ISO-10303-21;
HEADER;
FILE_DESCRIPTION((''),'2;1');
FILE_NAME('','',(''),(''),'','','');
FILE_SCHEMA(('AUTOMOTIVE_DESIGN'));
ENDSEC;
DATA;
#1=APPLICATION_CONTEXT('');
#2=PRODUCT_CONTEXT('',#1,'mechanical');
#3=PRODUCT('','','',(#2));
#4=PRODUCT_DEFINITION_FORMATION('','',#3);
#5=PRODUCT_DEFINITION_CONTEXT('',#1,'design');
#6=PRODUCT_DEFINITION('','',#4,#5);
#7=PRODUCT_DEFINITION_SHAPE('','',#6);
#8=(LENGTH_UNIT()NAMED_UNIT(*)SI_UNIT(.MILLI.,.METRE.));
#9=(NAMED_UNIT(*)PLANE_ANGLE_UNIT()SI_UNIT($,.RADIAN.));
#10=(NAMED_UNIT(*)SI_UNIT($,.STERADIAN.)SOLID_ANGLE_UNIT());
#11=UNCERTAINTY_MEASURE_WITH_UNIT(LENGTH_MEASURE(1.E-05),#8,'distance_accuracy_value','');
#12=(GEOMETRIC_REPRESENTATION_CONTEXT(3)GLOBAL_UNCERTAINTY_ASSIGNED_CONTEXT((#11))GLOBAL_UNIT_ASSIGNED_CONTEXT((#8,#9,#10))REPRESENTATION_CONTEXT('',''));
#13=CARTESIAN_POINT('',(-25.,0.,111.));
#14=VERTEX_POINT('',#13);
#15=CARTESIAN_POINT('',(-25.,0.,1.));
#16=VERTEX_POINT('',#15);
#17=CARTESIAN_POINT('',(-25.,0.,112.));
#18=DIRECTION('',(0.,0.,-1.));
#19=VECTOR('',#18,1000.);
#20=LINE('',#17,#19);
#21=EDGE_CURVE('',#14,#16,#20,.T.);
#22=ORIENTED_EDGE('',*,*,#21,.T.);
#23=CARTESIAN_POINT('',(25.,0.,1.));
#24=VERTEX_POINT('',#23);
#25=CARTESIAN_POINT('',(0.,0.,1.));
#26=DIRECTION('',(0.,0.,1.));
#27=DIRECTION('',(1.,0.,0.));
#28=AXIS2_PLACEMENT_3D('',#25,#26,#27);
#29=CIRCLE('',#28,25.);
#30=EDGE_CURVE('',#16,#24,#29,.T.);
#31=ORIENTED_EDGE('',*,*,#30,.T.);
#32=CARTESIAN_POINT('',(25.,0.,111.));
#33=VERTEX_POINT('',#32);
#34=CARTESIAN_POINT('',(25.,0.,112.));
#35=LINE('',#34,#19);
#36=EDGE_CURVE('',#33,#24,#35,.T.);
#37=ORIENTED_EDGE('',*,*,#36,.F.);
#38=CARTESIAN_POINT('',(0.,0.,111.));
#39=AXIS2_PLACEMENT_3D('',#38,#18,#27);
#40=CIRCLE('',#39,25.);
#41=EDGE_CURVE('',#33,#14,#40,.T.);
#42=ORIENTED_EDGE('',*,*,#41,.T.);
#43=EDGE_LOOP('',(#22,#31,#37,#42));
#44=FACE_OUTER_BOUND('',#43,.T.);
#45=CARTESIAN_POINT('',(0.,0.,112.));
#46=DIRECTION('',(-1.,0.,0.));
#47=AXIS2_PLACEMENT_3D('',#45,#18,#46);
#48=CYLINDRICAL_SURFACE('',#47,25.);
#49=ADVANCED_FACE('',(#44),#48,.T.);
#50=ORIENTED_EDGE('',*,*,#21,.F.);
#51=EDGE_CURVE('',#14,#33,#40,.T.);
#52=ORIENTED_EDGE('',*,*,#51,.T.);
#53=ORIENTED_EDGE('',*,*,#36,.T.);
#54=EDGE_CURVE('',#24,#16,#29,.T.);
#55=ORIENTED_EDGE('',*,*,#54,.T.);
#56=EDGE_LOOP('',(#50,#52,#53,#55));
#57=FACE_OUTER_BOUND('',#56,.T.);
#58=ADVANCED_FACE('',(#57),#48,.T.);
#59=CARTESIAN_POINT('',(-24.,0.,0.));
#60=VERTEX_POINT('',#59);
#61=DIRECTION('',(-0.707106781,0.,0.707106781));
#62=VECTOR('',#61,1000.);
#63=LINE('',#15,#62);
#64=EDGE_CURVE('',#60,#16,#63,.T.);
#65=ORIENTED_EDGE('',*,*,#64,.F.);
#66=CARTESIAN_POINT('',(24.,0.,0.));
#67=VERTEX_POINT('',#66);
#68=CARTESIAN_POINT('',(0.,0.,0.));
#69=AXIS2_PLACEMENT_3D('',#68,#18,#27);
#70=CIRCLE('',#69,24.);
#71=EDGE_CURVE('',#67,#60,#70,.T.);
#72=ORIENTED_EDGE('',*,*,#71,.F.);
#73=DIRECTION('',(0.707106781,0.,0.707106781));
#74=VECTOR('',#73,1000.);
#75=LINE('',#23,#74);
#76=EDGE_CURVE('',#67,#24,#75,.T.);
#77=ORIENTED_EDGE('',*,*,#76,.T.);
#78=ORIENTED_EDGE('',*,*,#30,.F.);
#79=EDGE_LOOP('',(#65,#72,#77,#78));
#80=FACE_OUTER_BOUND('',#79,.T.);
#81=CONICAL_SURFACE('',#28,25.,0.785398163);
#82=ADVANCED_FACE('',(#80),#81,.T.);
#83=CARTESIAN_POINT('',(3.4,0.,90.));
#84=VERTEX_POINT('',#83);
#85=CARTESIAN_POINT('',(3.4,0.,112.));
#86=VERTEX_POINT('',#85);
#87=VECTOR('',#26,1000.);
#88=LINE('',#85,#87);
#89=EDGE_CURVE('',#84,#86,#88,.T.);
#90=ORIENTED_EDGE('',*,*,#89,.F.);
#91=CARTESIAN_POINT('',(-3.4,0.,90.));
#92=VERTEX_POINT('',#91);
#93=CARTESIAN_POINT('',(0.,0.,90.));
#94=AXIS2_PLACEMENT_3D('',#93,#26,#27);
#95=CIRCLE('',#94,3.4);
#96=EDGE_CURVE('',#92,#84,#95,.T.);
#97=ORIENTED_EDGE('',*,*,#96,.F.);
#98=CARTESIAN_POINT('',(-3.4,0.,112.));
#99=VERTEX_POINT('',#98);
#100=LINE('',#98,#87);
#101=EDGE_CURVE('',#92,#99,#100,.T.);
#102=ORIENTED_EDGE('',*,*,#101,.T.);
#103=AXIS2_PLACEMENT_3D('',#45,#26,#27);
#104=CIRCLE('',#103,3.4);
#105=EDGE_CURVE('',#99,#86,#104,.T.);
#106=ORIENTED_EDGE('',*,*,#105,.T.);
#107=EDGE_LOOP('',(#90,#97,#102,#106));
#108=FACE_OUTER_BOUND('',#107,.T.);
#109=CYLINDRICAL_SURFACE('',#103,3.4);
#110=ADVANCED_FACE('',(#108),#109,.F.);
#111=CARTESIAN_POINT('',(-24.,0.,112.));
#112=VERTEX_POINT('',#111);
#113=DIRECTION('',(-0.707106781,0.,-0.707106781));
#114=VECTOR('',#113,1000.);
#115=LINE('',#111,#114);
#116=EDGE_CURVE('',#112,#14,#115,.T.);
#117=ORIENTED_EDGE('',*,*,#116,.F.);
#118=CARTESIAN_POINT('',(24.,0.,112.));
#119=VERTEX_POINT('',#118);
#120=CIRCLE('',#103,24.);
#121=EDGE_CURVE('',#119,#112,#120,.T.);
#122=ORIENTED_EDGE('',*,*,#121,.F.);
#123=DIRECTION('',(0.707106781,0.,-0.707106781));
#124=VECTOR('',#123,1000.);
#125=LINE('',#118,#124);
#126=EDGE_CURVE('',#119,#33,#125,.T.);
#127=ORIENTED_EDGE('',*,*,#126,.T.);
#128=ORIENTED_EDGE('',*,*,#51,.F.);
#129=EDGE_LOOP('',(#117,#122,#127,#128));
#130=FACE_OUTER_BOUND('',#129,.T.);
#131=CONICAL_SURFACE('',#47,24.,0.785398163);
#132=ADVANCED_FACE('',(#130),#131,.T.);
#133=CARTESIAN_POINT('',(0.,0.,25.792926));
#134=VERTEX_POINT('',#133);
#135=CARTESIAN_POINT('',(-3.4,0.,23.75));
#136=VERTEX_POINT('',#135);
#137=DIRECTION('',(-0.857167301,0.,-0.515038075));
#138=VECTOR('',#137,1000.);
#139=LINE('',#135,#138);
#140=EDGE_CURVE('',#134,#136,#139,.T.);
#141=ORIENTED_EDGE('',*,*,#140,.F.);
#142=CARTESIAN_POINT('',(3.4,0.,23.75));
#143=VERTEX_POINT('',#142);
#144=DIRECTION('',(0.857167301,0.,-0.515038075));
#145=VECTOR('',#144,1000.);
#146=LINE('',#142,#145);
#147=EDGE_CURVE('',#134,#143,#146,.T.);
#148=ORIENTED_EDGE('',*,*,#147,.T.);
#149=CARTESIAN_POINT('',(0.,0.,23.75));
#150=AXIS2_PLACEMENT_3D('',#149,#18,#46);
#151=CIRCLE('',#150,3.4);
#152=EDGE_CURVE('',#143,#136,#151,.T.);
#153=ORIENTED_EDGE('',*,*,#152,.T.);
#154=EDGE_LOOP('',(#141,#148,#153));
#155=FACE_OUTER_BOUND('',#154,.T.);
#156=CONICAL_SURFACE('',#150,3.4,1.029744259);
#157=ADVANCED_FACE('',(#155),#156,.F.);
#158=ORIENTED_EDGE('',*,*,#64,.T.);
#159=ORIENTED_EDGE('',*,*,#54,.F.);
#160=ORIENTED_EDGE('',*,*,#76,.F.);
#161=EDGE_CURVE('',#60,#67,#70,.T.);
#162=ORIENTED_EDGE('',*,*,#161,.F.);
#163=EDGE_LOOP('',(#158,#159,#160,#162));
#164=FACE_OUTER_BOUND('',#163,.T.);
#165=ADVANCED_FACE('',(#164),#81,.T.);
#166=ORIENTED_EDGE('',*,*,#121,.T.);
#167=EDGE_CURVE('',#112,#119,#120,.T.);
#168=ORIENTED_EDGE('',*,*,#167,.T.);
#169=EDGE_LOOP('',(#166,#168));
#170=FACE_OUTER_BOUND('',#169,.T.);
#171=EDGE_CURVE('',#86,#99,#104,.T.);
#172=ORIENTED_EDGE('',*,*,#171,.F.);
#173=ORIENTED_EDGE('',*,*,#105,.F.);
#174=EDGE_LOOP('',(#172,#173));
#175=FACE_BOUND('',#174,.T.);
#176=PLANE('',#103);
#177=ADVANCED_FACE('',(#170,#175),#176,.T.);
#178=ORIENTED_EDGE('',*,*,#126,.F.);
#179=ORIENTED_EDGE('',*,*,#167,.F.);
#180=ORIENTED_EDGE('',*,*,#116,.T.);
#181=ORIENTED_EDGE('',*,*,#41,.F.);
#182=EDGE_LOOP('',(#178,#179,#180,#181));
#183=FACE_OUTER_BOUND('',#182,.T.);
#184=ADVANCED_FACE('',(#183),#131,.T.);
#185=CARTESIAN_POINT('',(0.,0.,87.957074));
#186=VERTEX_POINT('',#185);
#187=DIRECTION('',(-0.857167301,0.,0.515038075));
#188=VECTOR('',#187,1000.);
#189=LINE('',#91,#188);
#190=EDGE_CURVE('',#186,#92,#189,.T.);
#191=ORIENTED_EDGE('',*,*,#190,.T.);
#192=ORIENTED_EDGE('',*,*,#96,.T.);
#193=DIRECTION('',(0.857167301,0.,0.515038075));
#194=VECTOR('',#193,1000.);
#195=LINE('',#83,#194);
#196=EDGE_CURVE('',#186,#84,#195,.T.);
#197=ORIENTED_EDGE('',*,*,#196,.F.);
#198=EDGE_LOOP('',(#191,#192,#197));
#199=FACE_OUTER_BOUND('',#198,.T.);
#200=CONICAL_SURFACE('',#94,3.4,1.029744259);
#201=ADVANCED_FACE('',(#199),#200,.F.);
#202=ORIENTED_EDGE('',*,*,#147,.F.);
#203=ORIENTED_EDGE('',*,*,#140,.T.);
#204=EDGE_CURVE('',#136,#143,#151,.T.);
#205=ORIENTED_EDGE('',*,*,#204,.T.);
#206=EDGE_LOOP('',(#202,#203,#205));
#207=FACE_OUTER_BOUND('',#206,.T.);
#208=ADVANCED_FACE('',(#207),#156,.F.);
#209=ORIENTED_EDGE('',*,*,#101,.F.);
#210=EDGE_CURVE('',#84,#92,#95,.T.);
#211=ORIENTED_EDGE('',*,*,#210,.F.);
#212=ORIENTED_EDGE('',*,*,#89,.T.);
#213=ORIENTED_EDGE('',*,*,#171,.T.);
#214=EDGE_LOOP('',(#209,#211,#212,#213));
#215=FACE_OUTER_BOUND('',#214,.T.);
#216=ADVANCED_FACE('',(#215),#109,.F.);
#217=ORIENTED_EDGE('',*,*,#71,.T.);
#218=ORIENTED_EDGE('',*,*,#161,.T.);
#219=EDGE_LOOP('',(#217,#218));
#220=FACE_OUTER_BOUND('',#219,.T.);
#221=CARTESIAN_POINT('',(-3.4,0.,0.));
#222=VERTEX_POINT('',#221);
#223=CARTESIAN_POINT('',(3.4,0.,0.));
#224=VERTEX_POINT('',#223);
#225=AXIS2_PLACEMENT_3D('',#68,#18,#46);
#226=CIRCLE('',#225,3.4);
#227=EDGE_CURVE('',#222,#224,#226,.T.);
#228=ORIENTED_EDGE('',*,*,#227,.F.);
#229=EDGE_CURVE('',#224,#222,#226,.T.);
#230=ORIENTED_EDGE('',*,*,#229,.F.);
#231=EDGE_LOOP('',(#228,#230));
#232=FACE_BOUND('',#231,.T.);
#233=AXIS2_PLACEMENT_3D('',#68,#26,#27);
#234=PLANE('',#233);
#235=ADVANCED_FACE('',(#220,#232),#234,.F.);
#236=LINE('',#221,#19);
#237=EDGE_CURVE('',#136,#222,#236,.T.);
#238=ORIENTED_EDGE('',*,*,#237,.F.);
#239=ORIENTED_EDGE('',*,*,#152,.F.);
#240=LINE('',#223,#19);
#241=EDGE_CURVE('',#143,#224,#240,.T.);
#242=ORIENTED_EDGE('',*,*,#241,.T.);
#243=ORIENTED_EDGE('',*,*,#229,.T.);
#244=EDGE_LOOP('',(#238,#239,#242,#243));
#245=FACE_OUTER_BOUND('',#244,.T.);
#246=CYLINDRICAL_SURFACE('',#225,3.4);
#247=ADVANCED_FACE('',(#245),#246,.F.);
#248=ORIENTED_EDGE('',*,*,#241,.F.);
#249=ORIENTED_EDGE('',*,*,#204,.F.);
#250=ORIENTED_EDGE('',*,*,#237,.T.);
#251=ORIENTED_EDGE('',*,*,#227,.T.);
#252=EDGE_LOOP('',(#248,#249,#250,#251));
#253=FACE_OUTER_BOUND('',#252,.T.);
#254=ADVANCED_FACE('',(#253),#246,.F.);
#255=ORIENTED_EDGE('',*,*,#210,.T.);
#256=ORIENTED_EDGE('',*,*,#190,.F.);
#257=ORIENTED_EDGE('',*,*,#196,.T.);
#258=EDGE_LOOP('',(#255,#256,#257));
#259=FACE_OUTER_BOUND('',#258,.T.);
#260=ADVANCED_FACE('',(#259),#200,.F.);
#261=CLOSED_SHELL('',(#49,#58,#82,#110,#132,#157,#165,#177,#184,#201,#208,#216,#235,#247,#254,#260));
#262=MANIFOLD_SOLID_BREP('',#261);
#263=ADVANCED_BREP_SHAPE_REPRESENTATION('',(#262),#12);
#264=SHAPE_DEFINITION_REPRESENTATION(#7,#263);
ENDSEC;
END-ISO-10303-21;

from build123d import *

# Parameters (mm, degrees)
SKETCH1_R             = 25
BOSS_EXTRUDE1_DEPTH   = 112
M8_TAPPED_HOLE1_D     = 6.8
M8_TAPPED_HOLE1_DEPTH = 22
M8_TAPPED_HOLE1_TIP   = 2.042926105
M8_TAPPED_HOLE2_D     = 6.8
M8_TAPPED_HOLE2_DEPTH = 23.75
M8_TAPPED_HOLE2_TIP   = 2.042926105
CHAMFER1_SIZE         = 1


with BuildPart() as part:
    # Sketch1 → Boss-Extrude1 (new body)
    with BuildSketch(Plane.XY):
        Circle(SKETCH1_R)
    extrude(amount=BOSS_EXTRUDE1_DEPTH)

    # M8 Tapped Hole1
    with Locations(Plane.XY.offset(112)):
        with Locations((0, 0)):
            Hole(M8_TAPPED_HOLE1_D / 2, depth=M8_TAPPED_HOLE1_DEPTH)
            with Locations((0, 0, -(M8_TAPPED_HOLE1_DEPTH + M8_TAPPED_HOLE1_TIP / 2))):  # 118° drill point
                Cone(0, M8_TAPPED_HOLE1_D / 2, M8_TAPPED_HOLE1_TIP, mode=Mode.SUBTRACT)

    # M8 Tapped Hole2
    with Locations(Plane(origin=(0, 0, 0), x_dir=(-1, 0, 0), z_dir=(0, 0, -1))):
        with Locations((0, 0)):
            Hole(M8_TAPPED_HOLE2_D / 2, depth=M8_TAPPED_HOLE2_DEPTH)
            with Locations((0, 0, -(M8_TAPPED_HOLE2_DEPTH + M8_TAPPED_HOLE2_TIP / 2))):  # 118° drill point
                Cone(0, M8_TAPPED_HOLE2_D / 2, M8_TAPPED_HOLE2_TIP, mode=Mode.SUBTRACT)

    # Chamfer1
    chamfer1_edges = [part.edges().sort_by_distance(p)[0] for p in [
        (-25, 0, 0),
        (-25, 0, 112),
    ]]
    chamfer(chamfer1_edges, length=CHAMFER1_SIZE)


solid = part.part
